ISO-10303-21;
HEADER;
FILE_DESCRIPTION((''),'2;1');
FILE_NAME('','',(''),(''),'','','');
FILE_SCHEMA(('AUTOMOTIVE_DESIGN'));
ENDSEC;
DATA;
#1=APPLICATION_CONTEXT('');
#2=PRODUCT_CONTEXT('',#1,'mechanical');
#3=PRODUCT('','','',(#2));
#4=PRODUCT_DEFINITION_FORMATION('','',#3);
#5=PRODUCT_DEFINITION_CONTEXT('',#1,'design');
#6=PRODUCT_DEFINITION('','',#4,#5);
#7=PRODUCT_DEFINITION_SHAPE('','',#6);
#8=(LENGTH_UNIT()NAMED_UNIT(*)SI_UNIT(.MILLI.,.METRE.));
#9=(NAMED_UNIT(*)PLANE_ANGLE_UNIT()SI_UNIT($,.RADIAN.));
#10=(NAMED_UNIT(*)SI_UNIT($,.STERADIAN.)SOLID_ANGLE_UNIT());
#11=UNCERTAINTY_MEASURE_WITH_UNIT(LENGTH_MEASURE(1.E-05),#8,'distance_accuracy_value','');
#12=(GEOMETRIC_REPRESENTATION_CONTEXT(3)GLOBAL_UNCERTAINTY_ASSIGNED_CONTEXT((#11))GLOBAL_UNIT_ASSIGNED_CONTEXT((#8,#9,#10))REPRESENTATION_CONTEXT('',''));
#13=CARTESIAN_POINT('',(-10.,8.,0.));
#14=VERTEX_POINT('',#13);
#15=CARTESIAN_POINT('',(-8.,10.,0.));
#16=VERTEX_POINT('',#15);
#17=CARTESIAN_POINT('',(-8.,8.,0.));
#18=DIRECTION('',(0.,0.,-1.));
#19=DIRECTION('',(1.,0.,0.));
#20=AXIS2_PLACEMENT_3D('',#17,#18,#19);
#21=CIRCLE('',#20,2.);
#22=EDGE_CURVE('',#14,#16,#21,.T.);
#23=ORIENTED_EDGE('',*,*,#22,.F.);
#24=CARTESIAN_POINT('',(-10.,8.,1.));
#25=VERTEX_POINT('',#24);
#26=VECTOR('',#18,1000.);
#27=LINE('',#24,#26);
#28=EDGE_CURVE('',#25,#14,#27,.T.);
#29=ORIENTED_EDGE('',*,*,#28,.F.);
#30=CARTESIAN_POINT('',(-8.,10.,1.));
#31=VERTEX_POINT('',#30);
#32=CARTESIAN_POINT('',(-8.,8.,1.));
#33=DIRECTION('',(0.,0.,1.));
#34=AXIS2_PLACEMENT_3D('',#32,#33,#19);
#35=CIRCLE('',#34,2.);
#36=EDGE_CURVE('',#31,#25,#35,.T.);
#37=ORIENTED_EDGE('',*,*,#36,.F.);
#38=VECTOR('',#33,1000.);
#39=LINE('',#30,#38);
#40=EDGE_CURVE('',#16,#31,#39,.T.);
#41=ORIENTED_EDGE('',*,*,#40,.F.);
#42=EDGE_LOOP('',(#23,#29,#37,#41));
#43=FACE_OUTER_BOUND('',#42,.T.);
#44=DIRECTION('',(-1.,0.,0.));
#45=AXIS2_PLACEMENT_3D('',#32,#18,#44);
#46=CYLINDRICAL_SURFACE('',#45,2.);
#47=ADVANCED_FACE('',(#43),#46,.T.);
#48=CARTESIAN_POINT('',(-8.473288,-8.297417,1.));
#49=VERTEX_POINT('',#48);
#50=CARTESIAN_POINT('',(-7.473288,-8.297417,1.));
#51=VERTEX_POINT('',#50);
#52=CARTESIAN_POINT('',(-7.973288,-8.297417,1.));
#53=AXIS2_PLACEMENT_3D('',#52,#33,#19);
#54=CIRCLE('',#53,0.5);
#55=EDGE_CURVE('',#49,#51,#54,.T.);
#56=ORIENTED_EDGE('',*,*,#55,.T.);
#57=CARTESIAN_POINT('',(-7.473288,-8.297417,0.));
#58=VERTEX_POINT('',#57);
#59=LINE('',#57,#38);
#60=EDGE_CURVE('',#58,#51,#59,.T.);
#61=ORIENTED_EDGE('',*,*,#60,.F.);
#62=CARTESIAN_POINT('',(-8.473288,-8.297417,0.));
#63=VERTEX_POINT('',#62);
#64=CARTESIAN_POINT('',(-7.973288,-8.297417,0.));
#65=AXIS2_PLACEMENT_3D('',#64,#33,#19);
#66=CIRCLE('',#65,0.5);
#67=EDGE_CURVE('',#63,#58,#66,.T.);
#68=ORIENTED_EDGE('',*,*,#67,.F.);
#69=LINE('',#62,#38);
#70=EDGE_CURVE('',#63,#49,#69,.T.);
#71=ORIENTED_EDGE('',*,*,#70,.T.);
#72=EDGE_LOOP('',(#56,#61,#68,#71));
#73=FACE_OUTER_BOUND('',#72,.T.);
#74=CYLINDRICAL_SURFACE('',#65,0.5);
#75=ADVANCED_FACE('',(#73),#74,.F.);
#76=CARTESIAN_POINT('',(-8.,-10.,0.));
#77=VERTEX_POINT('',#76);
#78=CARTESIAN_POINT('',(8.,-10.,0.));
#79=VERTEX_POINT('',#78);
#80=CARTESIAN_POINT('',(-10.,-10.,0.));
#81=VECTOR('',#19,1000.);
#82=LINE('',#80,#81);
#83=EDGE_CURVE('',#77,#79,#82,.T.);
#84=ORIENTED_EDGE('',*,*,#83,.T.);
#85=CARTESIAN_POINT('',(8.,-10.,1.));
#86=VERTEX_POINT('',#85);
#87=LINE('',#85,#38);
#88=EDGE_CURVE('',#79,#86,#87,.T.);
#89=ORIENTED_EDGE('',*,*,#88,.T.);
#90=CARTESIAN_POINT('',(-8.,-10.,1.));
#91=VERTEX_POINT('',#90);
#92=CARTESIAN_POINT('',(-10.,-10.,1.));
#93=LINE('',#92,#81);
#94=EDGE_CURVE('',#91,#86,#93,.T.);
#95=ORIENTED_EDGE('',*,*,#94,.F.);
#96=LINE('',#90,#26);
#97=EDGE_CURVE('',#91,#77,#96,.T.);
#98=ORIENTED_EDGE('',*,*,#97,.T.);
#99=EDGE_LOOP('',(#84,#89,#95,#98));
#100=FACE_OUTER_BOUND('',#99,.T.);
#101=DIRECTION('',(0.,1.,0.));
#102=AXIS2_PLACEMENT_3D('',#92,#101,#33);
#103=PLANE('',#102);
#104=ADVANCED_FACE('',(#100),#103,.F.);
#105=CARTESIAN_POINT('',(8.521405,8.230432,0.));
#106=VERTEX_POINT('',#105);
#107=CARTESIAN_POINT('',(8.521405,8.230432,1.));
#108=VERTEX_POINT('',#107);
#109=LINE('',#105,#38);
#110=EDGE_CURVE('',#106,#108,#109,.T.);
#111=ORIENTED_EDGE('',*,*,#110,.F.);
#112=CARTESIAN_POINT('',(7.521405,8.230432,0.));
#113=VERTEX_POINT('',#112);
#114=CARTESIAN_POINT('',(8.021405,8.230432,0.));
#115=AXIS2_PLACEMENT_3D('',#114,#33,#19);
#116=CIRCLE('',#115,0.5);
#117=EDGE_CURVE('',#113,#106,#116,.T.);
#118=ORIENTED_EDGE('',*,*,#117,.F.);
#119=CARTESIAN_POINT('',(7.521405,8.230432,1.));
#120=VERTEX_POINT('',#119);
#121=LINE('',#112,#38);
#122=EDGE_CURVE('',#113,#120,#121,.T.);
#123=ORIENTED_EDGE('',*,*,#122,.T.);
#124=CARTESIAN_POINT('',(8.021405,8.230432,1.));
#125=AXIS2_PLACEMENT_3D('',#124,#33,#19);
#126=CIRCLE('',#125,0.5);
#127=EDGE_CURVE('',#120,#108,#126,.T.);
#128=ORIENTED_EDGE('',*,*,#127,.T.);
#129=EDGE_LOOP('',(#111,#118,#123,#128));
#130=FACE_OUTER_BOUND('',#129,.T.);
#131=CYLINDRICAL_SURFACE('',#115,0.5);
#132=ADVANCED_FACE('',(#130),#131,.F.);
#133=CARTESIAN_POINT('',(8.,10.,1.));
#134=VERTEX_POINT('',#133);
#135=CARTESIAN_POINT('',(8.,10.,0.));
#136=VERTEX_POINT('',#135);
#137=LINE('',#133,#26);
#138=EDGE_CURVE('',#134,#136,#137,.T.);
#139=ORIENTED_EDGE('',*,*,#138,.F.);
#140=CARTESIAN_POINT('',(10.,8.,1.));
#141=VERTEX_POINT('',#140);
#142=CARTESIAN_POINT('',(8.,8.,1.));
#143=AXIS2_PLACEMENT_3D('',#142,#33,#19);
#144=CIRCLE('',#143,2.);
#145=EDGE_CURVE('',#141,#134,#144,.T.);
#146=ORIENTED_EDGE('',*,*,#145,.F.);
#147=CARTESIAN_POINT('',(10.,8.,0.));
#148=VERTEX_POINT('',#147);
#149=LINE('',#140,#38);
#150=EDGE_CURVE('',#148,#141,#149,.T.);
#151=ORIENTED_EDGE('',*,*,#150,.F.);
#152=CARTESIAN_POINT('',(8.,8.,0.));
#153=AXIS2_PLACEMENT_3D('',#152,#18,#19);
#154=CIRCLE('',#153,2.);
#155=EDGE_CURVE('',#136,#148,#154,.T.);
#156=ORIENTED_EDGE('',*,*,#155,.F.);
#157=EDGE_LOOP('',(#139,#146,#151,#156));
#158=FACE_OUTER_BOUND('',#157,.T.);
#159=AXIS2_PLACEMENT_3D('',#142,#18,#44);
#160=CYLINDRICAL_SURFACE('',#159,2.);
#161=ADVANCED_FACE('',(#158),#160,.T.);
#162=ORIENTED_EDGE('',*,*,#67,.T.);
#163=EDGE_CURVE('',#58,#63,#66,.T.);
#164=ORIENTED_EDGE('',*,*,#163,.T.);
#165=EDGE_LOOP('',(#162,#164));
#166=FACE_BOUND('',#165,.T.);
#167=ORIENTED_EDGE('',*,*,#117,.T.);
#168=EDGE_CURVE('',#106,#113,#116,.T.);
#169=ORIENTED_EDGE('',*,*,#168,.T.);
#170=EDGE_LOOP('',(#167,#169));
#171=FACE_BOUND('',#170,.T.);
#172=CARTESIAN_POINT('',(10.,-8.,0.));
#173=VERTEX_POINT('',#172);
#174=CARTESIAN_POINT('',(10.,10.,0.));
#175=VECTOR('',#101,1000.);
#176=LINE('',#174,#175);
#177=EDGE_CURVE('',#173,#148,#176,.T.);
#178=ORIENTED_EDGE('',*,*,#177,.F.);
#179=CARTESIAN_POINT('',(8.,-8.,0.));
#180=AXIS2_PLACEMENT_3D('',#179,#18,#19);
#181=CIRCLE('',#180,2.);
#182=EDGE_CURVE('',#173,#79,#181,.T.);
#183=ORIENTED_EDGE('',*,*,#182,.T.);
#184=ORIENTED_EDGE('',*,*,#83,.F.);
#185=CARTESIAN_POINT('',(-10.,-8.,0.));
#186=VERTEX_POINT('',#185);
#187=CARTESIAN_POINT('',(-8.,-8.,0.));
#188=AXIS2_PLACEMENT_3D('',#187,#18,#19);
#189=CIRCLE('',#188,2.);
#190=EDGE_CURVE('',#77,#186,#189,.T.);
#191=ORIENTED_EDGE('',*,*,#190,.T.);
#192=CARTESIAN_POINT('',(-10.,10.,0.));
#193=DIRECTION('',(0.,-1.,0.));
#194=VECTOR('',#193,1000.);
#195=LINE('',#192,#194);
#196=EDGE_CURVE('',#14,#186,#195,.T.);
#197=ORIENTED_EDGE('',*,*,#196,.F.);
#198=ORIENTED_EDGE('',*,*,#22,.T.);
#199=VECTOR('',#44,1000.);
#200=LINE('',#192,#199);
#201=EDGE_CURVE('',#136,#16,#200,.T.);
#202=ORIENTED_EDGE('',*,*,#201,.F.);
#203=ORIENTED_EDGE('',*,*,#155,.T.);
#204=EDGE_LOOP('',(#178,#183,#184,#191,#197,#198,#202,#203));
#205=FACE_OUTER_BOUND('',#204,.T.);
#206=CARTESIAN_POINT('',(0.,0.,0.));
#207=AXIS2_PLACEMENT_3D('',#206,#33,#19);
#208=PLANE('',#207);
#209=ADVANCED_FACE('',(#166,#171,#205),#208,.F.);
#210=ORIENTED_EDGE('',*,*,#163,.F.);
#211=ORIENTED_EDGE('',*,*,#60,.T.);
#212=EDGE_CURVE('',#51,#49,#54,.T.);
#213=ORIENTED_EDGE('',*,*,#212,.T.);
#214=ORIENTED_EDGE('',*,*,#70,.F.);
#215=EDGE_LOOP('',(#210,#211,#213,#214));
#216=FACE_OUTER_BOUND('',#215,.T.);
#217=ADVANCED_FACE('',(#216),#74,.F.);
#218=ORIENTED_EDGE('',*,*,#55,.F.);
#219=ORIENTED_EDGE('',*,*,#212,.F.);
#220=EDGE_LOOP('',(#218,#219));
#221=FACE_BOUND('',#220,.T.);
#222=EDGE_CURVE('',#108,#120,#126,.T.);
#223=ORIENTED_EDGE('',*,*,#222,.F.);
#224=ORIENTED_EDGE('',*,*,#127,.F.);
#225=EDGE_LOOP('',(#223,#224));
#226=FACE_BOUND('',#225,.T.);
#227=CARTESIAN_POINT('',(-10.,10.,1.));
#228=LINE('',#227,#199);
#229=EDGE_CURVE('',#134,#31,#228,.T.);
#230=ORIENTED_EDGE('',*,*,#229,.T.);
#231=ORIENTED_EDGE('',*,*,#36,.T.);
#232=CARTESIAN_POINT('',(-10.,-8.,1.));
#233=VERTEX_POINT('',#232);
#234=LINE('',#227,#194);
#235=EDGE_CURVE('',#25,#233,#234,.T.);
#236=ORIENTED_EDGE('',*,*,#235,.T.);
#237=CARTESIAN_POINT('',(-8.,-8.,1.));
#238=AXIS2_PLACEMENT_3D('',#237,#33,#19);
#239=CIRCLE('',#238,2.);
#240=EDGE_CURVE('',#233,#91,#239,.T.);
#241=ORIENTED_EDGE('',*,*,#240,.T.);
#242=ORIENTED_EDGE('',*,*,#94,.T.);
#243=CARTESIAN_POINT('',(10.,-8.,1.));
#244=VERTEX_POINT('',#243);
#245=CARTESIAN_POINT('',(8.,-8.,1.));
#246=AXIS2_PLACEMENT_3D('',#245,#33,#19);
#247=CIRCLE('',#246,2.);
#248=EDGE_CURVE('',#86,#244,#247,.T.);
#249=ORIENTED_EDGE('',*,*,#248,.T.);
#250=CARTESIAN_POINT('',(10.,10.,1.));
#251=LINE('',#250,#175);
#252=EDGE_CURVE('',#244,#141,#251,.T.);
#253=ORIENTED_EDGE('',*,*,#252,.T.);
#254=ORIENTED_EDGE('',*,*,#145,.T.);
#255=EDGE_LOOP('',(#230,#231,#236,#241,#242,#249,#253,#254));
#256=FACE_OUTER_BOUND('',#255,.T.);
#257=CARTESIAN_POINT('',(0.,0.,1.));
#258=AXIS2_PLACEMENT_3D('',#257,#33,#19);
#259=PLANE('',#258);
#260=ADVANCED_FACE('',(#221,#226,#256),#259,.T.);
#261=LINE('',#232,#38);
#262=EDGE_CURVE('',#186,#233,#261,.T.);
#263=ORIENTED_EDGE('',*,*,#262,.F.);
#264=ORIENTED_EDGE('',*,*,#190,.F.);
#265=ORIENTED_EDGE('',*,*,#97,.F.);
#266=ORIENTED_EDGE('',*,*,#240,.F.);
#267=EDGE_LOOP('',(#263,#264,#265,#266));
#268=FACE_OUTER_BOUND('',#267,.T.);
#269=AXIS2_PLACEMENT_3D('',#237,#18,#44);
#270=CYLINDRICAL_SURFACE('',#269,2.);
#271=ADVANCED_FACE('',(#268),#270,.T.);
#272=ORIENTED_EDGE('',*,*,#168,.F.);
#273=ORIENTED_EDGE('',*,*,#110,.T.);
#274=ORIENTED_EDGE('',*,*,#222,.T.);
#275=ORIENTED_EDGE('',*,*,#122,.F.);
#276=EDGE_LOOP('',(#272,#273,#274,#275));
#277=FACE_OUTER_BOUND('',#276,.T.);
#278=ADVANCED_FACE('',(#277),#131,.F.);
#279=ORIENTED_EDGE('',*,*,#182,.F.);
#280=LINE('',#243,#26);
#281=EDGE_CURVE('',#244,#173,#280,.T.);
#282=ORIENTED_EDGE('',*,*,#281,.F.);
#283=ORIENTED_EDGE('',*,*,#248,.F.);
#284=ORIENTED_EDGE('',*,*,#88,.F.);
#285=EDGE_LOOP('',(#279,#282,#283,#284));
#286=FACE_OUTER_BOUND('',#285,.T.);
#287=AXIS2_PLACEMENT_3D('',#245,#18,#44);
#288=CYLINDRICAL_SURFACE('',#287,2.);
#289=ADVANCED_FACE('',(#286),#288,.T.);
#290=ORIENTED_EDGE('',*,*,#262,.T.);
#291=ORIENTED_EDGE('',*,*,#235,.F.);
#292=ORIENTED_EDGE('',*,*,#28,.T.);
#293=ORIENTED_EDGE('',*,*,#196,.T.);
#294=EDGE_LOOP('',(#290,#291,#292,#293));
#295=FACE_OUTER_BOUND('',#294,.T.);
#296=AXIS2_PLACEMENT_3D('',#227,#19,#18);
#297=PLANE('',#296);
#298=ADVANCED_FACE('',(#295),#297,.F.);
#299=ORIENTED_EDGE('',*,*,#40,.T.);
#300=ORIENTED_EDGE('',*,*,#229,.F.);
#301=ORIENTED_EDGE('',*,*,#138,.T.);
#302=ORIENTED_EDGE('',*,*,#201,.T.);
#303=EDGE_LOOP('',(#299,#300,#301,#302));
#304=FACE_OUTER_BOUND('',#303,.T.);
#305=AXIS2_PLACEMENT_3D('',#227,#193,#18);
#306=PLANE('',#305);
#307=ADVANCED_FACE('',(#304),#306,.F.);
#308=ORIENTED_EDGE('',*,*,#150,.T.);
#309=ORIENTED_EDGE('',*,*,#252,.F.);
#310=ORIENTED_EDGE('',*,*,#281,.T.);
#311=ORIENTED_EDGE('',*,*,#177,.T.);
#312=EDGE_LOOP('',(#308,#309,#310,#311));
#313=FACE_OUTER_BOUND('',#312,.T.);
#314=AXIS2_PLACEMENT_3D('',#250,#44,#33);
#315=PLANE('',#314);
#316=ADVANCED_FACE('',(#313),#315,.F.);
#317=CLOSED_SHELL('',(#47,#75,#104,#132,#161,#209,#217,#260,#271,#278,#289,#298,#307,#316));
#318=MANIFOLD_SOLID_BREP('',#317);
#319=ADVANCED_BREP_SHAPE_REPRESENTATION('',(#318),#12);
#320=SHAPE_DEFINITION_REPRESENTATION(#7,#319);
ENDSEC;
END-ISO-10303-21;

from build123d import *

# Parameters (mm, degrees)
SKETCH1_W           = 20
SKETCH1_H           = 20
BOSS_EXTRUDE1_DEPTH = 1
SKETCH2_R           = 0.5
CUT_EXTRUDE1_DEPTH  = 15.177446879
FILLET1_R           = 2


with BuildPart() as part:
    # Sketch1 → Boss-Extrude1 (new body)
    with BuildSketch(Plane.XY):
        Rectangle(SKETCH1_W, SKETCH1_H)
    extrude(amount=BOSS_EXTRUDE1_DEPTH)

    # Sketch2 → Cut-Extrude1 (cut, through all)
    with BuildSketch(Plane.XY.offset(1)):
        with Locations((-7.973287509, -8.297417088)):
            Circle(SKETCH2_R)
        with Locations((8.021405324, 8.230432172)):
            Circle(SKETCH2_R)
    extrude(amount=-CUT_EXTRUDE1_DEPTH, mode=Mode.SUBTRACT)

    # Fillet1
    fillet1_edges = [part.edges().sort_by_distance(p)[0] for p in [
        (10, -10, 0.5),
        (-10, -10, 0.5),
        (-10, 10, 0.5),
        (10, 10, 0.5),
    ]]
    fillet(fillet1_edges, radius=FILLET1_R)


solid = part.part
